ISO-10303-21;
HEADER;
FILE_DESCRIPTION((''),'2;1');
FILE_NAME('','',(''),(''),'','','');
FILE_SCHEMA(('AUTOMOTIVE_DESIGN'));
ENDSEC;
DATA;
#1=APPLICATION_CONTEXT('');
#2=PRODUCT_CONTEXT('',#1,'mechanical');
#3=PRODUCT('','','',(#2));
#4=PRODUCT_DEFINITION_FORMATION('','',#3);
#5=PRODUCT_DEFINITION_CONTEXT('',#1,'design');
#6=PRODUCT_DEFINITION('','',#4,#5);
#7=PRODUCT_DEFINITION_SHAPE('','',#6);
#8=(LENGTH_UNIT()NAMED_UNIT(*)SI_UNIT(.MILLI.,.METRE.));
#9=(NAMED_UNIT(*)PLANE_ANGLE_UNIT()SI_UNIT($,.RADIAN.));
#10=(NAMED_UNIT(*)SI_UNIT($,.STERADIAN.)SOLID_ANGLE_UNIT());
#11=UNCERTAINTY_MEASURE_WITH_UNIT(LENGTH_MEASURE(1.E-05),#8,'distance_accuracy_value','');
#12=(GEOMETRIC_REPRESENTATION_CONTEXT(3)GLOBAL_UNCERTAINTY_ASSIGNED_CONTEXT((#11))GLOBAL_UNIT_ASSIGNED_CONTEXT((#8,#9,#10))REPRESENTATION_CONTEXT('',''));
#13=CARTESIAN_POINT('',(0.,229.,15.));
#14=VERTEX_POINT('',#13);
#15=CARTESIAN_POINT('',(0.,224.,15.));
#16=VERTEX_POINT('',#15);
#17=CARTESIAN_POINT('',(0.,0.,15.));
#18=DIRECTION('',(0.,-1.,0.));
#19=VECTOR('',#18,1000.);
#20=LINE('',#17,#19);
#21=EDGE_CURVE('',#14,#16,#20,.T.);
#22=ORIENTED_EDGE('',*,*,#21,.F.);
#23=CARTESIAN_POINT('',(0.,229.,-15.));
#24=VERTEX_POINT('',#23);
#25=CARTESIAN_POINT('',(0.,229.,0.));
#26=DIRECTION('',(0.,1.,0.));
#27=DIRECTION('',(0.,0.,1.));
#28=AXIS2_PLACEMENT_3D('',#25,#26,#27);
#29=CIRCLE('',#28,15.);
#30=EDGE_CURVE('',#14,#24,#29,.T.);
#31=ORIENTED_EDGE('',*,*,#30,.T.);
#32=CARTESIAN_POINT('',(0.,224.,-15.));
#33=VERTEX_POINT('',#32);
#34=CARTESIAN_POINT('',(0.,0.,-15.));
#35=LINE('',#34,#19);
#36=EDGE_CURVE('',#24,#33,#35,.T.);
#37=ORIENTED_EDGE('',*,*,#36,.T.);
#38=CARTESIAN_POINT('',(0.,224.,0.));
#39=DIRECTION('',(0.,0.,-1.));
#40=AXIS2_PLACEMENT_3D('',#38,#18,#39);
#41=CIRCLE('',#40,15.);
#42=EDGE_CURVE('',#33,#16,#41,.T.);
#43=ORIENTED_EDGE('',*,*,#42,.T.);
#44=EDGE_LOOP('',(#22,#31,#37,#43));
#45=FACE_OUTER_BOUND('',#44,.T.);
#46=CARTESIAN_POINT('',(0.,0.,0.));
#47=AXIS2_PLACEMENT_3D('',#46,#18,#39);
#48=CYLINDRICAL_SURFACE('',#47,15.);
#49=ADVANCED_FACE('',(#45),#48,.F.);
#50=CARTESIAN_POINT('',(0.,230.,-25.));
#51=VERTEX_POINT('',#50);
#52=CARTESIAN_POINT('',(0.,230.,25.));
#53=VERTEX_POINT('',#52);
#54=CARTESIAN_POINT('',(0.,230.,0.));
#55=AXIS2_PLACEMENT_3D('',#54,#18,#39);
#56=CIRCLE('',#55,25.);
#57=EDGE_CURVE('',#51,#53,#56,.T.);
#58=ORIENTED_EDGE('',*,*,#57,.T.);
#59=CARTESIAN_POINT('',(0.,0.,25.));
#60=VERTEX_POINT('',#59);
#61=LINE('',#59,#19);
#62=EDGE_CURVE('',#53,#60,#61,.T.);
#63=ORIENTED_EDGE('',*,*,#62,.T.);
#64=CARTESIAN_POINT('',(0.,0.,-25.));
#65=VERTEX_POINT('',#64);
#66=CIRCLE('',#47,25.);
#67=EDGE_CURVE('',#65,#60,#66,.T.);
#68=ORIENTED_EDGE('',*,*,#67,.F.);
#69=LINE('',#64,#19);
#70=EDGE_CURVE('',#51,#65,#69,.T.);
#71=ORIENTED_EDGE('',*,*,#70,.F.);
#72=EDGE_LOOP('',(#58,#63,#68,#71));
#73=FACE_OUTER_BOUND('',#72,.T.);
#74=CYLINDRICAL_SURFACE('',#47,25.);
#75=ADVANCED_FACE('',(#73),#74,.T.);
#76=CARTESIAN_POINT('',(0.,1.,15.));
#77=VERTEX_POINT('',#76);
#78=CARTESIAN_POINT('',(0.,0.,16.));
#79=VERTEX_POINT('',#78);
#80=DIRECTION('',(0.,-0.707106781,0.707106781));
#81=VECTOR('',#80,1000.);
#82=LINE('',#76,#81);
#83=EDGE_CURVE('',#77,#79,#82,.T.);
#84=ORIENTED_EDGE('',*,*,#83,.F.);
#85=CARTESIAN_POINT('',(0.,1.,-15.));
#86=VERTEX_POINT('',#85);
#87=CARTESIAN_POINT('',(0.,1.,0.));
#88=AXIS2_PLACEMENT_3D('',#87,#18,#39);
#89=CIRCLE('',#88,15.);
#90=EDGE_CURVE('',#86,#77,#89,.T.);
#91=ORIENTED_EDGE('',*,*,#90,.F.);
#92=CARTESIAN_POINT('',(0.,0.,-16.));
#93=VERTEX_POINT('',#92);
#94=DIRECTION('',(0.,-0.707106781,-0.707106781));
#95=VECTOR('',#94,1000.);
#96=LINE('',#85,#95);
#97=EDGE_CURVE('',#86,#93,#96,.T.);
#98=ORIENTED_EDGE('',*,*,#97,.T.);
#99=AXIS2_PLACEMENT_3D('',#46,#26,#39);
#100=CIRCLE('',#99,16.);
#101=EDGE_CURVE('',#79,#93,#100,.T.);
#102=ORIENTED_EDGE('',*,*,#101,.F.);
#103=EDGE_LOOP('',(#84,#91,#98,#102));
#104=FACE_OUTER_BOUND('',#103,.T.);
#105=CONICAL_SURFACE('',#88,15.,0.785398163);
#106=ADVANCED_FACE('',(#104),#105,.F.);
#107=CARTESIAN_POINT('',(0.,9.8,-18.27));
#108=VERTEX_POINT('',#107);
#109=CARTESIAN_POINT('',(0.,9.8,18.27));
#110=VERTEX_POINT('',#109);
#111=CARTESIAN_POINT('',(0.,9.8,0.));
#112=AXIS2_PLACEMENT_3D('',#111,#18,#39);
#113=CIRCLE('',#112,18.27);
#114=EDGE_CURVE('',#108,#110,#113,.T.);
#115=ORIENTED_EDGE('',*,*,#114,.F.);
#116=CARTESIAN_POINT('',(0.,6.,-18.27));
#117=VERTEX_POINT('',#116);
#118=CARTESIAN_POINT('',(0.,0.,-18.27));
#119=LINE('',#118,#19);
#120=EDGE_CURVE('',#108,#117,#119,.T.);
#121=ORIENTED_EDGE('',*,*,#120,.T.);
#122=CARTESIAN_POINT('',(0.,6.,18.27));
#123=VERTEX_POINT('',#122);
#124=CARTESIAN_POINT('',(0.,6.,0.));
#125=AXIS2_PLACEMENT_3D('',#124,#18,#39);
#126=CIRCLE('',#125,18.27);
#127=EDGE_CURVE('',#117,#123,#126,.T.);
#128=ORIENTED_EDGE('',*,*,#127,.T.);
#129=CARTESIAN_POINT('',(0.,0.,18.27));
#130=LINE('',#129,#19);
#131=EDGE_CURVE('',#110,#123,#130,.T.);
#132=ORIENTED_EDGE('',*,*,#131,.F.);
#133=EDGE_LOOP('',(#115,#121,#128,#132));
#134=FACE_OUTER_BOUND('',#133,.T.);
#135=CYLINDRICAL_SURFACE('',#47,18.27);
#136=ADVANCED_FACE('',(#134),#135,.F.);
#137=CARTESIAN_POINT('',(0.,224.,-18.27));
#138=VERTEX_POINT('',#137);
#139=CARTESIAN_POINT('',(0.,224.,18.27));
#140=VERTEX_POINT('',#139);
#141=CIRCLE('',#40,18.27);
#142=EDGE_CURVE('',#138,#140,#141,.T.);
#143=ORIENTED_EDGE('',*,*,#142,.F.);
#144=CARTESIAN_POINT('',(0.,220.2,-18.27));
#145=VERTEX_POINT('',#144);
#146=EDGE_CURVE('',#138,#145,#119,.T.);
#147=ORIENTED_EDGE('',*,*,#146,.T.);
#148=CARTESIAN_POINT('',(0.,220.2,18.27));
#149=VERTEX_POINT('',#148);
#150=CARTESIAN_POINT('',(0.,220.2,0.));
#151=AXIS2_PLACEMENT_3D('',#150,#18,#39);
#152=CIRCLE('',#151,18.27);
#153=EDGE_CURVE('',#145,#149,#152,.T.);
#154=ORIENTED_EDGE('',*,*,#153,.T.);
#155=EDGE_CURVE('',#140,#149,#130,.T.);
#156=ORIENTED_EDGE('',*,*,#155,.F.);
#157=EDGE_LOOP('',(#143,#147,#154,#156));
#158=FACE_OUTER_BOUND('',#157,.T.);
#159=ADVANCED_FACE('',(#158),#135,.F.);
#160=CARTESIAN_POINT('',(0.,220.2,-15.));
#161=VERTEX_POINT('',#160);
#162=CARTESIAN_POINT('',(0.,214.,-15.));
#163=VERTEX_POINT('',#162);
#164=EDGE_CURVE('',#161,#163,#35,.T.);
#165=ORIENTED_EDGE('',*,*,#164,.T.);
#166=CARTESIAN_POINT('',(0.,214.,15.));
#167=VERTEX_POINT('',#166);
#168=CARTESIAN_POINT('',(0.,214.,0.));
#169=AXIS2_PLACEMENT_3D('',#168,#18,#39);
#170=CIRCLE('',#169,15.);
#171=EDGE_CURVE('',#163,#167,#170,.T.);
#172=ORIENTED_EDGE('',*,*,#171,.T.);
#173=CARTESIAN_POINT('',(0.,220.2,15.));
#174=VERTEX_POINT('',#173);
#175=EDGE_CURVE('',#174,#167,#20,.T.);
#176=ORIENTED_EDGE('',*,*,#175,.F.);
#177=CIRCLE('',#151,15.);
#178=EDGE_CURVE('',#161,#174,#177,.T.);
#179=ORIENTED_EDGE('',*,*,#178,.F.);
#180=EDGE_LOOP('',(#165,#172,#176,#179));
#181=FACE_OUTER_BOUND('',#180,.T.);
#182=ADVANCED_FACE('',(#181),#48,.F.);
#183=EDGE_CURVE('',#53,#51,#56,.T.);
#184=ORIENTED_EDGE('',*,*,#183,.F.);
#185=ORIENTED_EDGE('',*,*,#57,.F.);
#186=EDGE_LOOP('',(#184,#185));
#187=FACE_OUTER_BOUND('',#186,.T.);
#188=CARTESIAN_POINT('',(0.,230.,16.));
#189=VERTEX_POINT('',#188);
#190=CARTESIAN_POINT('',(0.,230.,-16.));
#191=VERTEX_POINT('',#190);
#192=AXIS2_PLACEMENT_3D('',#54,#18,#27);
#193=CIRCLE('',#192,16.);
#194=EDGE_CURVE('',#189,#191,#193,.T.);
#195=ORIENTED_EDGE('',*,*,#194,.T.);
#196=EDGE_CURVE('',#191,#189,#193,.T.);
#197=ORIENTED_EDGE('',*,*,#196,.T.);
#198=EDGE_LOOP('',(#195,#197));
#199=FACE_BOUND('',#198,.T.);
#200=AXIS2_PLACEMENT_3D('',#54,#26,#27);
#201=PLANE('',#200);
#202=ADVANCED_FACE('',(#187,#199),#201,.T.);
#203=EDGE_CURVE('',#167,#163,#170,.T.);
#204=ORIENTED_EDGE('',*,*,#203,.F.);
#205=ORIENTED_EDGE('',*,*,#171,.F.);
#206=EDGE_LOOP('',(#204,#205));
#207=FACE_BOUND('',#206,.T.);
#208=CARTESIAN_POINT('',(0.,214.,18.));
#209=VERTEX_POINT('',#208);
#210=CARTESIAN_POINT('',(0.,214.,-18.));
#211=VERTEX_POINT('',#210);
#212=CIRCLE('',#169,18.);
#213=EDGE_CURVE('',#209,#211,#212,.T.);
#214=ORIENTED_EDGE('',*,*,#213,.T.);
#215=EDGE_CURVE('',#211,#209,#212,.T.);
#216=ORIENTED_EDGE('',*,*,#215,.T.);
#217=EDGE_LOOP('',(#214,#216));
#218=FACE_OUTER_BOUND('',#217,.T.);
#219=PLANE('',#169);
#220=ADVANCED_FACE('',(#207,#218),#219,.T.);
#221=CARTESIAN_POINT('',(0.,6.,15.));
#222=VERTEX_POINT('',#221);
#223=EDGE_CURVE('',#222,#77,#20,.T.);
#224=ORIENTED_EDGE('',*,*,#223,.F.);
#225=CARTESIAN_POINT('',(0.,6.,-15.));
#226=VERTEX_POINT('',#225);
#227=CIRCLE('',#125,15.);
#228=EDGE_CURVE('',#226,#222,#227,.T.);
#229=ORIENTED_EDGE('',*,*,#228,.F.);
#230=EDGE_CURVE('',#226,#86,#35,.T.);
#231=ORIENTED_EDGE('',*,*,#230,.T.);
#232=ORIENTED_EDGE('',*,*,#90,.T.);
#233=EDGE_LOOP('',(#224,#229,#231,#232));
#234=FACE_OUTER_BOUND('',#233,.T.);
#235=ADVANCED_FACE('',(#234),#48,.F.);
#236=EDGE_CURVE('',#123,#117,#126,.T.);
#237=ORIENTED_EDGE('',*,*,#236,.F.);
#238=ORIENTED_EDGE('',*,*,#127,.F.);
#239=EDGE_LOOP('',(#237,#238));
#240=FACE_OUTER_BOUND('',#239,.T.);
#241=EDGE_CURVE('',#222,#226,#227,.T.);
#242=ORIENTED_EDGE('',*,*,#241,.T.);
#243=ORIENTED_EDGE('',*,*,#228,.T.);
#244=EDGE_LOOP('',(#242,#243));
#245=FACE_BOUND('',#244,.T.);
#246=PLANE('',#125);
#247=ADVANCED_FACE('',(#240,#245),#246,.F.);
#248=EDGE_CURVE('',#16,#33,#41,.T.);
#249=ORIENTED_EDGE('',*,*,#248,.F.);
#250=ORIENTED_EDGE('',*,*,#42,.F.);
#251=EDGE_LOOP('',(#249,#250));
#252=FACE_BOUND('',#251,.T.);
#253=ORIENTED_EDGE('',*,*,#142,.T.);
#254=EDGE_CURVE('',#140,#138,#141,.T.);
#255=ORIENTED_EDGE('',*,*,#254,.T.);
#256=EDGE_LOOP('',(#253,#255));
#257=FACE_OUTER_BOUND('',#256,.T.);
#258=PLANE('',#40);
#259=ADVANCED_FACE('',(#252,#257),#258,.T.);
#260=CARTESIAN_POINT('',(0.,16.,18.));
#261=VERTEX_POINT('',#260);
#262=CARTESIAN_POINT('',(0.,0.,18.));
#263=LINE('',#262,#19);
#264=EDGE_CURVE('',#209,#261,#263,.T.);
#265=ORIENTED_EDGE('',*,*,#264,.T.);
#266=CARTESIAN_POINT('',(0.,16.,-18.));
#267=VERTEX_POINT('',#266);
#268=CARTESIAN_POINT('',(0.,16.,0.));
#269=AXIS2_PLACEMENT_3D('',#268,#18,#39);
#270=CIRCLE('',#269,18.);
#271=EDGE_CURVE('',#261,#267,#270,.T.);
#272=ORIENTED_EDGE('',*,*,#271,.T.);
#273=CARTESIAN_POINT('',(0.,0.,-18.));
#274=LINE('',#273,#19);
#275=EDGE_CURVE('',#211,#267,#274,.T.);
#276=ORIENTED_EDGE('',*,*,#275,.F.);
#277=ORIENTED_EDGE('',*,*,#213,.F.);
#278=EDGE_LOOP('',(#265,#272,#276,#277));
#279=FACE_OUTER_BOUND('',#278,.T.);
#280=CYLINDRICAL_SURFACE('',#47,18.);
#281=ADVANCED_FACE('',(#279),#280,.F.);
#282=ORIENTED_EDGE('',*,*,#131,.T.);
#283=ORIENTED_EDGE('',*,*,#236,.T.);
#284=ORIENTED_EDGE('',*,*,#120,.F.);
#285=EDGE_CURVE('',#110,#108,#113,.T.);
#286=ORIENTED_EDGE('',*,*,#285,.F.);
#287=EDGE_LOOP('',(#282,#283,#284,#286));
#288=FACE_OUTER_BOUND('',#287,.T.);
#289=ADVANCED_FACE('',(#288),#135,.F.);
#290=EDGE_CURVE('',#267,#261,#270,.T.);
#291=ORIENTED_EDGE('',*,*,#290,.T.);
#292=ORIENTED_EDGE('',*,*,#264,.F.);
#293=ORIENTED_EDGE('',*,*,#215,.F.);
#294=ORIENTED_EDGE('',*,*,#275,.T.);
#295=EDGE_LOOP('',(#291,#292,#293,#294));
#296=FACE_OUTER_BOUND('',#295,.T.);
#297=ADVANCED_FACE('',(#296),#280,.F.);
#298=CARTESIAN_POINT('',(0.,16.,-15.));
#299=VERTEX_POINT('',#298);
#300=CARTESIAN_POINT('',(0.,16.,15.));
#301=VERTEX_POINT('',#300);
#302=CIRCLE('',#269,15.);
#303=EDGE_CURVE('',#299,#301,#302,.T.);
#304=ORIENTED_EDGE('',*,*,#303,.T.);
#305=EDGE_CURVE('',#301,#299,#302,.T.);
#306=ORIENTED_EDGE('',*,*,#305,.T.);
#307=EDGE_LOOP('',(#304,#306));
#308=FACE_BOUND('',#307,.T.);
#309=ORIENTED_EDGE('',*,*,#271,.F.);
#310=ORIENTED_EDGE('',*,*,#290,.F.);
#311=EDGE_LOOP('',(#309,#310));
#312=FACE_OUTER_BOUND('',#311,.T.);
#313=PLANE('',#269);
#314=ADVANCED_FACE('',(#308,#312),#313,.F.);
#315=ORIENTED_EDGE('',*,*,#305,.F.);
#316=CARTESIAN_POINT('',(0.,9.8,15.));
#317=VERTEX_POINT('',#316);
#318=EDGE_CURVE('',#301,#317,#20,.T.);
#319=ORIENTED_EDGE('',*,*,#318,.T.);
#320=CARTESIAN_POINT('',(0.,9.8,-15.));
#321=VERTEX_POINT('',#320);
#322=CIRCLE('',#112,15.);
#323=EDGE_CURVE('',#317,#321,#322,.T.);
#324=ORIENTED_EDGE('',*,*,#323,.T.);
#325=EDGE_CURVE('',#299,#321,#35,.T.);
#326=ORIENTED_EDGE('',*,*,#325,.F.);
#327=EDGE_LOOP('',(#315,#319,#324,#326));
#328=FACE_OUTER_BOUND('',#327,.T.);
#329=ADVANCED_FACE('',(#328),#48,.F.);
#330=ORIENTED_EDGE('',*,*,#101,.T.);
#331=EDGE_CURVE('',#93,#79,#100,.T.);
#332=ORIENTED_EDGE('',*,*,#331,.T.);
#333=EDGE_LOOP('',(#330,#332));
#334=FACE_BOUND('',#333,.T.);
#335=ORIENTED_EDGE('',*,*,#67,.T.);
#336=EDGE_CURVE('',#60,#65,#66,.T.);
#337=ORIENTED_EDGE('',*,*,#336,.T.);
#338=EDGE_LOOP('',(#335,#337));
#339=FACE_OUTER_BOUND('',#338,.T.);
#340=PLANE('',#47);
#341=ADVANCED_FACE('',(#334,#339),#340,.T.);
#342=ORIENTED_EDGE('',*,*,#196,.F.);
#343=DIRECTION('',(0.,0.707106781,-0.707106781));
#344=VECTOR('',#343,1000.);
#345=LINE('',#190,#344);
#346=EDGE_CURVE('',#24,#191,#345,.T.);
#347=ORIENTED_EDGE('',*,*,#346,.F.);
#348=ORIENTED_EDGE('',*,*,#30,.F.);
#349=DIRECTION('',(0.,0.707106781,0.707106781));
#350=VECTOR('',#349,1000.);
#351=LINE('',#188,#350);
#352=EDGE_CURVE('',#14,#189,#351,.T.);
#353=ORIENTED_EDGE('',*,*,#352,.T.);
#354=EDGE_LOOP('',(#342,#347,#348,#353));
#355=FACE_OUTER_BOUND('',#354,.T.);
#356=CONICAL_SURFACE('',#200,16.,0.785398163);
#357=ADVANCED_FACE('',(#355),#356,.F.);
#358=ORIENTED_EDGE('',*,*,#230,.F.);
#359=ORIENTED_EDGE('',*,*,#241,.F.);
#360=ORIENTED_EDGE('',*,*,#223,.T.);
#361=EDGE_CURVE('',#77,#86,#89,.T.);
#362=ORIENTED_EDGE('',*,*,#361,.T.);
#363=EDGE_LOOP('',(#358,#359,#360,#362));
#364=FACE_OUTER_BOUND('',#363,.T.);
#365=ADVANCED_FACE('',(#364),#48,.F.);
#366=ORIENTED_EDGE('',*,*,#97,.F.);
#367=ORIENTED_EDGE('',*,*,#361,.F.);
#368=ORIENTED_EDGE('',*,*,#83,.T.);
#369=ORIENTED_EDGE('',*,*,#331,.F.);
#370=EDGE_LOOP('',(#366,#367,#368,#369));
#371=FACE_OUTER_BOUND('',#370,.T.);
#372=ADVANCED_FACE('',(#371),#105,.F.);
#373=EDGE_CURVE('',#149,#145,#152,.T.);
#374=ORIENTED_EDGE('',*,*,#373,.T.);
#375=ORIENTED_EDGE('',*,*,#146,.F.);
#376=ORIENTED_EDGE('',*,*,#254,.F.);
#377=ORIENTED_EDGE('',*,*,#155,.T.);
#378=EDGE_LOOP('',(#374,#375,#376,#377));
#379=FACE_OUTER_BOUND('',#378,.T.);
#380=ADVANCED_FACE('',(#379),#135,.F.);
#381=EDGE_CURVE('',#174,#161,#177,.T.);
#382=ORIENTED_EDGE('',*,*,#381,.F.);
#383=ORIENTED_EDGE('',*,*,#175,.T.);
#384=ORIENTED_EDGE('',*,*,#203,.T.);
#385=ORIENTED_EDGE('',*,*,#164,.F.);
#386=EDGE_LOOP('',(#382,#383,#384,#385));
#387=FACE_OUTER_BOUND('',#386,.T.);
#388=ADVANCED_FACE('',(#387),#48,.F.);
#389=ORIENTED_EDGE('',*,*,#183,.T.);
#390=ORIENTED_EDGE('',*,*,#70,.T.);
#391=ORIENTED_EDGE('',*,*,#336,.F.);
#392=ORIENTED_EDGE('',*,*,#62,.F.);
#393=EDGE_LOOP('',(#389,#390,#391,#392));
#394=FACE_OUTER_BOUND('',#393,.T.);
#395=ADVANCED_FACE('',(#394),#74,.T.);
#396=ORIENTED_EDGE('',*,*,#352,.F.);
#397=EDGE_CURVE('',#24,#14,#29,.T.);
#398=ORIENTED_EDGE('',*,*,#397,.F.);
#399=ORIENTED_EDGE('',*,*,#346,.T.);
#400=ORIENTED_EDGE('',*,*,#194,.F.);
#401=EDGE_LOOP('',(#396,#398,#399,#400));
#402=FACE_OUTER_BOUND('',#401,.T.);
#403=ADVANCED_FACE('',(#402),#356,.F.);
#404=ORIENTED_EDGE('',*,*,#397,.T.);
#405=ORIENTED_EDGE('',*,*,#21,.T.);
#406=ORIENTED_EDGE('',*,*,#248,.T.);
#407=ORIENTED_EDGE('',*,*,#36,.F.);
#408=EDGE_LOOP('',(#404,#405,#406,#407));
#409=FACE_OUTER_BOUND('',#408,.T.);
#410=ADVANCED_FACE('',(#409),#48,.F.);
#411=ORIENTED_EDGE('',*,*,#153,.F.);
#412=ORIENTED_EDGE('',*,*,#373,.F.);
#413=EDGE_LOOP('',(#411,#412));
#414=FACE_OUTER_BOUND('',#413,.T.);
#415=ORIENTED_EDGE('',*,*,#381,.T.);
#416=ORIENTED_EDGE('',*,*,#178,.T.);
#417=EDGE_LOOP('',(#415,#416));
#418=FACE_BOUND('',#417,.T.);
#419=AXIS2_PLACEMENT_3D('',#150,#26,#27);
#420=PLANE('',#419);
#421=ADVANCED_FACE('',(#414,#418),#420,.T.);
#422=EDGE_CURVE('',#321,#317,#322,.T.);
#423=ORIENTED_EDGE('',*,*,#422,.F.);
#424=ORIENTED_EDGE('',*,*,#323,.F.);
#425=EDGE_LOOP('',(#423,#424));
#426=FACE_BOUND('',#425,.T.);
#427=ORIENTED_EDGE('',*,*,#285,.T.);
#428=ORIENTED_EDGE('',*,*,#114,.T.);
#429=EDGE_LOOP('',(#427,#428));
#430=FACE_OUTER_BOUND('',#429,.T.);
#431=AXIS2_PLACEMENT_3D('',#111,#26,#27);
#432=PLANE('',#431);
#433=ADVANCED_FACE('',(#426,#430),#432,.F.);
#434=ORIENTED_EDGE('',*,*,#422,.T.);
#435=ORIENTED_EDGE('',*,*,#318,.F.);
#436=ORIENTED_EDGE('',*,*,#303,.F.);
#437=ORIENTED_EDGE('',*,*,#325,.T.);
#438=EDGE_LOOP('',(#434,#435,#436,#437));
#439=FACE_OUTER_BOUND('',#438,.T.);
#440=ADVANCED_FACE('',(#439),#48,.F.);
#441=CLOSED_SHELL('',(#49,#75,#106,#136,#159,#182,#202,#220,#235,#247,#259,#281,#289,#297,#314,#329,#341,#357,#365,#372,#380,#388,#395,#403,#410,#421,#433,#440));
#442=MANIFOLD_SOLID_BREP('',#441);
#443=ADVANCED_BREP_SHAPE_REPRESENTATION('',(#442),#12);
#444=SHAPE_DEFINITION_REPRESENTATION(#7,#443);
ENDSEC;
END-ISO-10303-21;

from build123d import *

# Parameters (mm, degrees)
CHAMFER_1_SIZE = 1


with BuildPart() as part:
    # 草图1 → 旋转1 (revolve)
    with BuildSketch(Plane.XY, mode=Mode.PRIVATE) as revolve_1_sk:
        Polygon((15, 6), (15, 0), (25, 0), (25, 230), (15, 230), (15, 224), (18.27, 224), (18.27, 220.2), (15, 220.2), (15, 214), (18, 214), (18, 16), (15, 16), (15, 9.8), (18.27, 9.8), (18.27, 6), align=None)
    revolve(revolve_1_sk.sketch.rotate(Axis((0, 0, 0), (0, 1, 0)), 90), axis=Axis((0, 0, 0), (0, 1, 0)))

    # 倒角1
    chamfer_1_edges = [part.edges().sort_by_distance(p)[0] for p in [
        (0, 230, 15),
        (0, 0, 15),
    ]]
    chamfer(chamfer_1_edges, length=CHAMFER_1_SIZE)


solid = part.part
